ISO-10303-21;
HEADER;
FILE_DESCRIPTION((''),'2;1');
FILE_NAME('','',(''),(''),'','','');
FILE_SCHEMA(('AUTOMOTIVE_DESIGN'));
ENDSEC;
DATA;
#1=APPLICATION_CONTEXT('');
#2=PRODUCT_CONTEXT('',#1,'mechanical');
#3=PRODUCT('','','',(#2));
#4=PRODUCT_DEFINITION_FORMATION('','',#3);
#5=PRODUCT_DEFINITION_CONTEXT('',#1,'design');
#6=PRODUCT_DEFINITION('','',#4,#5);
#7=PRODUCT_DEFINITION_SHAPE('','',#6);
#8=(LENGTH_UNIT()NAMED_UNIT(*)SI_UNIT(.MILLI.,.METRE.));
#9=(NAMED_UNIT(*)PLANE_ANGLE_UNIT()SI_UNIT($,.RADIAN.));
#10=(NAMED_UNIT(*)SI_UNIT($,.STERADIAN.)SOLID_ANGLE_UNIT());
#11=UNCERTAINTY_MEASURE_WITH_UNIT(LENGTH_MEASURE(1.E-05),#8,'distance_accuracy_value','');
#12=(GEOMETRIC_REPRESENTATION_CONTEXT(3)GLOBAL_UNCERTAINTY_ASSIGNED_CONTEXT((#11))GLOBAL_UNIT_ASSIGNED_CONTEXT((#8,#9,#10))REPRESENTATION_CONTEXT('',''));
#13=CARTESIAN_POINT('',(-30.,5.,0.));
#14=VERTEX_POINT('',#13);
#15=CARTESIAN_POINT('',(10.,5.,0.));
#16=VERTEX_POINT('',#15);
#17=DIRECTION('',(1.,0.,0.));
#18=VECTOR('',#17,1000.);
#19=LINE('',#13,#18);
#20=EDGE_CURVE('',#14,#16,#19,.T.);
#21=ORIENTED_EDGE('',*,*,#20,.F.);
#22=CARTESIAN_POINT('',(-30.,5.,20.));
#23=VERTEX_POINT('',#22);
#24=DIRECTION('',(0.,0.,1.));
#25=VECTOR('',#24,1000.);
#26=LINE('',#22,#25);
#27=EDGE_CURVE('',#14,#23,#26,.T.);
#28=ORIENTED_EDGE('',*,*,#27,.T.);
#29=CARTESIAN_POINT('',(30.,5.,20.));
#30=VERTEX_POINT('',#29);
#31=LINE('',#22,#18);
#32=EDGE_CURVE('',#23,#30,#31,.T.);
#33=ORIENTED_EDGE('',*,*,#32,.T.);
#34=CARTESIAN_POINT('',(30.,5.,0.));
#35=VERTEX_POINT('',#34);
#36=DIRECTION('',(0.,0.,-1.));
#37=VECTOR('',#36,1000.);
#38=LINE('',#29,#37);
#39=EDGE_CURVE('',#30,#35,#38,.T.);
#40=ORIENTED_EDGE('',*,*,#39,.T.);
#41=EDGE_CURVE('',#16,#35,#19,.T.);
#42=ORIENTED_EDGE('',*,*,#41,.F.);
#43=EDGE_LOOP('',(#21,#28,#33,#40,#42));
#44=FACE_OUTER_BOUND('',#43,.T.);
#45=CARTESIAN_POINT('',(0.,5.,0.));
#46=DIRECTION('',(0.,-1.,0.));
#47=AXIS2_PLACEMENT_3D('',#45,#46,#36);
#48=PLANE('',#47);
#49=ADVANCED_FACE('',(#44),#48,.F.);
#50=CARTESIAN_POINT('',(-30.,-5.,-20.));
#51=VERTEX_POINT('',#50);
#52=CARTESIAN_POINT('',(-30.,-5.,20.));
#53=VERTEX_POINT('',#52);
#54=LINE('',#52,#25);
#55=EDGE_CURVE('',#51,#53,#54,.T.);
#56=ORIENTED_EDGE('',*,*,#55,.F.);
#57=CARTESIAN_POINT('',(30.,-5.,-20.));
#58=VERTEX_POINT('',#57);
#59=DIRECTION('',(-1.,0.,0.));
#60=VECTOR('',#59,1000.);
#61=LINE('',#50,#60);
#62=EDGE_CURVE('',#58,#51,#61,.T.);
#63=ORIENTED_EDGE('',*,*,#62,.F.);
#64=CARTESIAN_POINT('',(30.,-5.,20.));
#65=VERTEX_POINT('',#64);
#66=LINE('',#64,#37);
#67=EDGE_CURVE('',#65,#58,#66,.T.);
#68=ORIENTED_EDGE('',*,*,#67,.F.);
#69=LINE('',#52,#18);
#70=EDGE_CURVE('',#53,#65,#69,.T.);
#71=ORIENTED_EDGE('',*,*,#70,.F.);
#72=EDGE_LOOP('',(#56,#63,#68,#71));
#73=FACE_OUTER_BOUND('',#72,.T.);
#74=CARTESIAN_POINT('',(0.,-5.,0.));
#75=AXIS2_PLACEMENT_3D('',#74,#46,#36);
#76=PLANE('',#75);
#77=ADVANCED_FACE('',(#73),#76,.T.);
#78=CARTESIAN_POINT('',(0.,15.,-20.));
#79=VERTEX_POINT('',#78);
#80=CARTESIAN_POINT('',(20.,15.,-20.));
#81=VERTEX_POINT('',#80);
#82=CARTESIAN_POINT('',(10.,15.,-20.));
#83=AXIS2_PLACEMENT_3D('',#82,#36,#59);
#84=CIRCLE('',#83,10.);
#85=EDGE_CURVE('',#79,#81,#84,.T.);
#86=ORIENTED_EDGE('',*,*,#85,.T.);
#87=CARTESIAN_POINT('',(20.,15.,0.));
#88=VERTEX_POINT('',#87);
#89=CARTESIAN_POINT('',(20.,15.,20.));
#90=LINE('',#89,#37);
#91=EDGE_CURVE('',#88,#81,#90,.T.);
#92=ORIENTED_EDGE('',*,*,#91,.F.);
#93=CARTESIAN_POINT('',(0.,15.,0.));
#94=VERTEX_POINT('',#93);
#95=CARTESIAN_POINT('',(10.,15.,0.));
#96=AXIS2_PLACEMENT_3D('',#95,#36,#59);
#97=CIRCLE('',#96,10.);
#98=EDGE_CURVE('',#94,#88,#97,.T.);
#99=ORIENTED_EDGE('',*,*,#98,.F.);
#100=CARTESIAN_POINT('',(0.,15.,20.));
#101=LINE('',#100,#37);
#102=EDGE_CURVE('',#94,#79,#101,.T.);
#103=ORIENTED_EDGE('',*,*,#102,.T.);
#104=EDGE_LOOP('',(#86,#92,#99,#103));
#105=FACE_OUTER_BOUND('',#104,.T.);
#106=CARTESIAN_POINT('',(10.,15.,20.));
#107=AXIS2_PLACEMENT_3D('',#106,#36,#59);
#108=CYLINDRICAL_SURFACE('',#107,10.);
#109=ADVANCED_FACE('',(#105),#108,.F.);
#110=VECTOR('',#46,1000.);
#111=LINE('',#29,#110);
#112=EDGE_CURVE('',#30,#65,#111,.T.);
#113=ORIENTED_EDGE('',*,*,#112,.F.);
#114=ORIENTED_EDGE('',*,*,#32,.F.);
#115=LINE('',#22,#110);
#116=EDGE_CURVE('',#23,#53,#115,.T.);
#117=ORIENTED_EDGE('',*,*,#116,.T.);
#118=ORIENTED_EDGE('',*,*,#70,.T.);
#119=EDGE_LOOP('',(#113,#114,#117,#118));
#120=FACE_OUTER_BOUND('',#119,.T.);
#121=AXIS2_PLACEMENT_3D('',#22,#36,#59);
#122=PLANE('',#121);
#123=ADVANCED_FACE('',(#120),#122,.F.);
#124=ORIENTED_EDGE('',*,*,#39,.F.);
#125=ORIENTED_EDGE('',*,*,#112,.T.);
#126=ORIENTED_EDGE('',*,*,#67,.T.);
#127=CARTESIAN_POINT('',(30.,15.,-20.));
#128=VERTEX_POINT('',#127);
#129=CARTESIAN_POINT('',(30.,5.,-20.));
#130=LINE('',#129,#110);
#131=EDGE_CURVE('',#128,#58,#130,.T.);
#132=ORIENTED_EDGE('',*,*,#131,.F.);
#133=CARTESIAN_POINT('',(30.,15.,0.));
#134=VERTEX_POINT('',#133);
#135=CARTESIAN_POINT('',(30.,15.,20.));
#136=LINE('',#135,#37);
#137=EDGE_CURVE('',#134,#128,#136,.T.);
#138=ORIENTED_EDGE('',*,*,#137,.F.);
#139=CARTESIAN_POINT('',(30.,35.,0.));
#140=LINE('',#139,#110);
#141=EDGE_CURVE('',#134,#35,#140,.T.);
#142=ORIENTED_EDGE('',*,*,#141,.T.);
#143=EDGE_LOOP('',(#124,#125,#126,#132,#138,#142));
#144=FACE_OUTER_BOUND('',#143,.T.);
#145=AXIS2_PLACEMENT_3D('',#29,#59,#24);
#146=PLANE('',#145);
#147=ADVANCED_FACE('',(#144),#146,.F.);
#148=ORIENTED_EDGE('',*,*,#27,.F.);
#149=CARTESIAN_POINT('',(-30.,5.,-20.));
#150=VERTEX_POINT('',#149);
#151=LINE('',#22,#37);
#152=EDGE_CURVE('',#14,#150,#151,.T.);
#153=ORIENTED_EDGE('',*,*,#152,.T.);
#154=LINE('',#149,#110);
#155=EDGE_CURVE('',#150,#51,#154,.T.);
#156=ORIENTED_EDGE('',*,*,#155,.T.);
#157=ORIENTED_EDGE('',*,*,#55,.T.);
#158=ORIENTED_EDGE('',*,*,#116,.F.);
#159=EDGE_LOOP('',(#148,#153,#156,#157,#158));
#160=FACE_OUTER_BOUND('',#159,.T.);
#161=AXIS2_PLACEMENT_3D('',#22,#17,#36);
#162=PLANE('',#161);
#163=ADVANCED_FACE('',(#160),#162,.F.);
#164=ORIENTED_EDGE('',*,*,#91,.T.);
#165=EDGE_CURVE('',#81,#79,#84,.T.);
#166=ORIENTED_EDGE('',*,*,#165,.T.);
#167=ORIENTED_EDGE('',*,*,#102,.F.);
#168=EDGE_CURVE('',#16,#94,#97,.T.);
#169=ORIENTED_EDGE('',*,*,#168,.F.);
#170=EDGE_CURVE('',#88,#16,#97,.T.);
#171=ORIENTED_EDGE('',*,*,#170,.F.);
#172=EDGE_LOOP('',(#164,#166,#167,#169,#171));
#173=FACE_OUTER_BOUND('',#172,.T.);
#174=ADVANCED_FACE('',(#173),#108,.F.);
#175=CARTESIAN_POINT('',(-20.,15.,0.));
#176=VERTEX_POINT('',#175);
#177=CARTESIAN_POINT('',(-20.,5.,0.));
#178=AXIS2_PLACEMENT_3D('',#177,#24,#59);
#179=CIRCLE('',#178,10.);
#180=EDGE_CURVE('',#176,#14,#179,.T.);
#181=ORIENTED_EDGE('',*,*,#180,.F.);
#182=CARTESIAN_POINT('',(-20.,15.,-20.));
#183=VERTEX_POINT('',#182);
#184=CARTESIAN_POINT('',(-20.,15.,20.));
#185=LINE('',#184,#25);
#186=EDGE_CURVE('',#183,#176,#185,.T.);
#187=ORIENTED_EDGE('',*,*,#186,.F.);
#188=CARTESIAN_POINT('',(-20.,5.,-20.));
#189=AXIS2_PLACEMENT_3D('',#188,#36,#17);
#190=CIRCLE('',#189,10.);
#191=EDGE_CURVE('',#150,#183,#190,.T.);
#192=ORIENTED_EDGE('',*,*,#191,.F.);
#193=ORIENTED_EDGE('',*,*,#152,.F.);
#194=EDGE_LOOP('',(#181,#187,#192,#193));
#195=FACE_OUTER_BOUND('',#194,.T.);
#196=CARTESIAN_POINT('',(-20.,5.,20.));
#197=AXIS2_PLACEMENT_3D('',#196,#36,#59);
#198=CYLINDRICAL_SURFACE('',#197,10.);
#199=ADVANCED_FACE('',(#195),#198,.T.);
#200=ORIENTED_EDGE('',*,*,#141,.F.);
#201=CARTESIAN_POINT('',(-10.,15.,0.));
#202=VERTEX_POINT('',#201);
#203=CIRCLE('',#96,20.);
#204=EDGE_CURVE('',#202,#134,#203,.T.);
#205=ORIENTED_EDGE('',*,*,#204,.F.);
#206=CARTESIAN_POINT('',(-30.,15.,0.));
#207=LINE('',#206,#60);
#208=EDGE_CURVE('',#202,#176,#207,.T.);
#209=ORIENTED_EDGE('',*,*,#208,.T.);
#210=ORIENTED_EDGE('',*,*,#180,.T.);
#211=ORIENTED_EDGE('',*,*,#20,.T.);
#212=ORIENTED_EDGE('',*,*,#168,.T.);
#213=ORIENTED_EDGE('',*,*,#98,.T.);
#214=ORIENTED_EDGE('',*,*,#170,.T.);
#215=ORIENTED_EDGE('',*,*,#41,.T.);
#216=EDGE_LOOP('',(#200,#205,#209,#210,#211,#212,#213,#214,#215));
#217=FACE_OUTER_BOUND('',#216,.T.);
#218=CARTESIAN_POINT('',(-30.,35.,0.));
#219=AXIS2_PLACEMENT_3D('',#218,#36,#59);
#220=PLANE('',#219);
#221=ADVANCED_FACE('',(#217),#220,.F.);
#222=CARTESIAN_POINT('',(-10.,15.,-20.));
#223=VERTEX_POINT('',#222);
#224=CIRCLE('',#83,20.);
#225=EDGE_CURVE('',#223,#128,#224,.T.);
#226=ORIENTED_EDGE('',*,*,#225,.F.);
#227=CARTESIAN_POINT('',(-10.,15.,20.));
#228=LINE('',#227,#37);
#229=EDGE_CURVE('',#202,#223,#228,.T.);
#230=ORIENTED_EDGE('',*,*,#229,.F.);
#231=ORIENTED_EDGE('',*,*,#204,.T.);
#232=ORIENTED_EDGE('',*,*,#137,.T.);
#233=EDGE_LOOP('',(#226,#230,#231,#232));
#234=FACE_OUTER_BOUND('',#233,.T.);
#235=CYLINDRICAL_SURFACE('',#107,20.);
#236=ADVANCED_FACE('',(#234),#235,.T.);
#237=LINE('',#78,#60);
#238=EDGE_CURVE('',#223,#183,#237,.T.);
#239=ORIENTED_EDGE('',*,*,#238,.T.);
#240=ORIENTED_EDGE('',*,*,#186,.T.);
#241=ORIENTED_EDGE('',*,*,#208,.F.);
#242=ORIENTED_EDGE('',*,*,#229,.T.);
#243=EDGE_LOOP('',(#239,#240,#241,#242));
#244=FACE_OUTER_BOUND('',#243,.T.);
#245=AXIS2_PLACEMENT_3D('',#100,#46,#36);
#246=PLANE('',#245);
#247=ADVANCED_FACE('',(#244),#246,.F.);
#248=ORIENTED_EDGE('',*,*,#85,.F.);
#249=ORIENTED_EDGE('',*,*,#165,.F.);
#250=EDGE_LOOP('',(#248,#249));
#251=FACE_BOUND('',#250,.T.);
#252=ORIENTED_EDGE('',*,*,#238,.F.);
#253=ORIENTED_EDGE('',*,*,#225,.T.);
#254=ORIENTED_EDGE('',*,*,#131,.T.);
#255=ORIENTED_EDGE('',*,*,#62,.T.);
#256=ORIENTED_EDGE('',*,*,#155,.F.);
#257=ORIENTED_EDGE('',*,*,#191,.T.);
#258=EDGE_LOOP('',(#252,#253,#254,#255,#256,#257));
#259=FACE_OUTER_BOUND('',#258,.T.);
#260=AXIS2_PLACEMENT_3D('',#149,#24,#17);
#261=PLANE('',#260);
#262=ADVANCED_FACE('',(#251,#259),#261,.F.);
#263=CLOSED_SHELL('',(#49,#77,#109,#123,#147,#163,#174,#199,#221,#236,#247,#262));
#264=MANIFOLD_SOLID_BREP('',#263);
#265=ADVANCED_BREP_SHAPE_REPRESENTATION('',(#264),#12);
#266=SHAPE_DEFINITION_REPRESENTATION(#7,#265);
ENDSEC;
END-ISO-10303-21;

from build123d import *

# Parameters (mm, degrees)
BASE_PLATE_SKETCH_W       = 60
BASE_PLATE_SKETCH_H       = 40
BASE_PLATE_60X40X10_DEPTH = 5
UPRIGHT_LUG_SKETCH_W      = 60
UPRIGHT_LUG_SKETCH_H      = 20
UPRIGHT_LUG_DEPTH         = 30
CROSS_HOLE_SKETCH_R       = 10
CROSS_HOLE_CUT_DEPTH      = 62.032778079
LUG_PROFILE_CUT_DEPTH     = 62.032778079
LUG_ROUND_R10_R           = 10


with BuildPart() as part:
    # Base Plate Sketch → Base Plate 60x40x10 (new, symmetric)
    with BuildSketch(Plane(origin=(0, 0, 0), x_dir=(1, 0, 0), z_dir=(0, 1, 0))):
        Rectangle(BASE_PLATE_SKETCH_W, BASE_PLATE_SKETCH_H)
    extrude(amount=BASE_PLATE_60X40X10_DEPTH, both=True)

    # Upright Lug Sketch → Upright Lug (add)
    with BuildSketch(Plane(origin=(0, 5, 0), x_dir=(1, 0, 0), z_dir=(0, 1, 0))):
        with Locations((0, 10)):
            Rectangle(UPRIGHT_LUG_SKETCH_W, UPRIGHT_LUG_SKETCH_H)
    extrude(amount=UPRIGHT_LUG_DEPTH)

    # Cross Hole Sketch → Cross Hole Cut (cut, through all)
    with BuildSketch(Plane(origin=(0, 0, -20), x_dir=(-1, 0, 0), z_dir=(0, 0, -1))):
        with Locations((-10, 15)):
            Circle(CROSS_HOLE_SKETCH_R)
    extrude(amount=-CROSS_HOLE_CUT_DEPTH, mode=Mode.SUBTRACT)

    # Lug Profile Sketch → Lug Profile Cut (cut, through all)
    with BuildSketch(Plane(origin=(0, 0, -20), x_dir=(-1, 0, 0), z_dir=(0, 0, -1))):
        with BuildLine():
            Line((-30, 35), (-30, 15.000000101))
            ThreePointArc((-30, 15.000000101), (-24.142135638, 29.142135609), (-10.000000142, 35))
            Line((-10.000000142, 35), (-30, 35))
        make_face()
        with BuildLine():
            ThreePointArc((-10.000000142, 35), (4.142135574, 29.142135674), (10, 15))
            Line((10, 15), (30, 15))
            Line((30, 15), (30, 35))
            Line((30, 35), (-10.000000142, 35))
        make_face()
    extrude(amount=-LUG_PROFILE_CUT_DEPTH, mode=Mode.SUBTRACT)

    # Lug Round R10
    lug_round_r10_edges = [part.edges().sort_by_distance(p)[0] for p in [
        (-30, 15, -10),
    ]]
    fillet(lug_round_r10_edges, radius=LUG_ROUND_R10_R)


solid = part.part
